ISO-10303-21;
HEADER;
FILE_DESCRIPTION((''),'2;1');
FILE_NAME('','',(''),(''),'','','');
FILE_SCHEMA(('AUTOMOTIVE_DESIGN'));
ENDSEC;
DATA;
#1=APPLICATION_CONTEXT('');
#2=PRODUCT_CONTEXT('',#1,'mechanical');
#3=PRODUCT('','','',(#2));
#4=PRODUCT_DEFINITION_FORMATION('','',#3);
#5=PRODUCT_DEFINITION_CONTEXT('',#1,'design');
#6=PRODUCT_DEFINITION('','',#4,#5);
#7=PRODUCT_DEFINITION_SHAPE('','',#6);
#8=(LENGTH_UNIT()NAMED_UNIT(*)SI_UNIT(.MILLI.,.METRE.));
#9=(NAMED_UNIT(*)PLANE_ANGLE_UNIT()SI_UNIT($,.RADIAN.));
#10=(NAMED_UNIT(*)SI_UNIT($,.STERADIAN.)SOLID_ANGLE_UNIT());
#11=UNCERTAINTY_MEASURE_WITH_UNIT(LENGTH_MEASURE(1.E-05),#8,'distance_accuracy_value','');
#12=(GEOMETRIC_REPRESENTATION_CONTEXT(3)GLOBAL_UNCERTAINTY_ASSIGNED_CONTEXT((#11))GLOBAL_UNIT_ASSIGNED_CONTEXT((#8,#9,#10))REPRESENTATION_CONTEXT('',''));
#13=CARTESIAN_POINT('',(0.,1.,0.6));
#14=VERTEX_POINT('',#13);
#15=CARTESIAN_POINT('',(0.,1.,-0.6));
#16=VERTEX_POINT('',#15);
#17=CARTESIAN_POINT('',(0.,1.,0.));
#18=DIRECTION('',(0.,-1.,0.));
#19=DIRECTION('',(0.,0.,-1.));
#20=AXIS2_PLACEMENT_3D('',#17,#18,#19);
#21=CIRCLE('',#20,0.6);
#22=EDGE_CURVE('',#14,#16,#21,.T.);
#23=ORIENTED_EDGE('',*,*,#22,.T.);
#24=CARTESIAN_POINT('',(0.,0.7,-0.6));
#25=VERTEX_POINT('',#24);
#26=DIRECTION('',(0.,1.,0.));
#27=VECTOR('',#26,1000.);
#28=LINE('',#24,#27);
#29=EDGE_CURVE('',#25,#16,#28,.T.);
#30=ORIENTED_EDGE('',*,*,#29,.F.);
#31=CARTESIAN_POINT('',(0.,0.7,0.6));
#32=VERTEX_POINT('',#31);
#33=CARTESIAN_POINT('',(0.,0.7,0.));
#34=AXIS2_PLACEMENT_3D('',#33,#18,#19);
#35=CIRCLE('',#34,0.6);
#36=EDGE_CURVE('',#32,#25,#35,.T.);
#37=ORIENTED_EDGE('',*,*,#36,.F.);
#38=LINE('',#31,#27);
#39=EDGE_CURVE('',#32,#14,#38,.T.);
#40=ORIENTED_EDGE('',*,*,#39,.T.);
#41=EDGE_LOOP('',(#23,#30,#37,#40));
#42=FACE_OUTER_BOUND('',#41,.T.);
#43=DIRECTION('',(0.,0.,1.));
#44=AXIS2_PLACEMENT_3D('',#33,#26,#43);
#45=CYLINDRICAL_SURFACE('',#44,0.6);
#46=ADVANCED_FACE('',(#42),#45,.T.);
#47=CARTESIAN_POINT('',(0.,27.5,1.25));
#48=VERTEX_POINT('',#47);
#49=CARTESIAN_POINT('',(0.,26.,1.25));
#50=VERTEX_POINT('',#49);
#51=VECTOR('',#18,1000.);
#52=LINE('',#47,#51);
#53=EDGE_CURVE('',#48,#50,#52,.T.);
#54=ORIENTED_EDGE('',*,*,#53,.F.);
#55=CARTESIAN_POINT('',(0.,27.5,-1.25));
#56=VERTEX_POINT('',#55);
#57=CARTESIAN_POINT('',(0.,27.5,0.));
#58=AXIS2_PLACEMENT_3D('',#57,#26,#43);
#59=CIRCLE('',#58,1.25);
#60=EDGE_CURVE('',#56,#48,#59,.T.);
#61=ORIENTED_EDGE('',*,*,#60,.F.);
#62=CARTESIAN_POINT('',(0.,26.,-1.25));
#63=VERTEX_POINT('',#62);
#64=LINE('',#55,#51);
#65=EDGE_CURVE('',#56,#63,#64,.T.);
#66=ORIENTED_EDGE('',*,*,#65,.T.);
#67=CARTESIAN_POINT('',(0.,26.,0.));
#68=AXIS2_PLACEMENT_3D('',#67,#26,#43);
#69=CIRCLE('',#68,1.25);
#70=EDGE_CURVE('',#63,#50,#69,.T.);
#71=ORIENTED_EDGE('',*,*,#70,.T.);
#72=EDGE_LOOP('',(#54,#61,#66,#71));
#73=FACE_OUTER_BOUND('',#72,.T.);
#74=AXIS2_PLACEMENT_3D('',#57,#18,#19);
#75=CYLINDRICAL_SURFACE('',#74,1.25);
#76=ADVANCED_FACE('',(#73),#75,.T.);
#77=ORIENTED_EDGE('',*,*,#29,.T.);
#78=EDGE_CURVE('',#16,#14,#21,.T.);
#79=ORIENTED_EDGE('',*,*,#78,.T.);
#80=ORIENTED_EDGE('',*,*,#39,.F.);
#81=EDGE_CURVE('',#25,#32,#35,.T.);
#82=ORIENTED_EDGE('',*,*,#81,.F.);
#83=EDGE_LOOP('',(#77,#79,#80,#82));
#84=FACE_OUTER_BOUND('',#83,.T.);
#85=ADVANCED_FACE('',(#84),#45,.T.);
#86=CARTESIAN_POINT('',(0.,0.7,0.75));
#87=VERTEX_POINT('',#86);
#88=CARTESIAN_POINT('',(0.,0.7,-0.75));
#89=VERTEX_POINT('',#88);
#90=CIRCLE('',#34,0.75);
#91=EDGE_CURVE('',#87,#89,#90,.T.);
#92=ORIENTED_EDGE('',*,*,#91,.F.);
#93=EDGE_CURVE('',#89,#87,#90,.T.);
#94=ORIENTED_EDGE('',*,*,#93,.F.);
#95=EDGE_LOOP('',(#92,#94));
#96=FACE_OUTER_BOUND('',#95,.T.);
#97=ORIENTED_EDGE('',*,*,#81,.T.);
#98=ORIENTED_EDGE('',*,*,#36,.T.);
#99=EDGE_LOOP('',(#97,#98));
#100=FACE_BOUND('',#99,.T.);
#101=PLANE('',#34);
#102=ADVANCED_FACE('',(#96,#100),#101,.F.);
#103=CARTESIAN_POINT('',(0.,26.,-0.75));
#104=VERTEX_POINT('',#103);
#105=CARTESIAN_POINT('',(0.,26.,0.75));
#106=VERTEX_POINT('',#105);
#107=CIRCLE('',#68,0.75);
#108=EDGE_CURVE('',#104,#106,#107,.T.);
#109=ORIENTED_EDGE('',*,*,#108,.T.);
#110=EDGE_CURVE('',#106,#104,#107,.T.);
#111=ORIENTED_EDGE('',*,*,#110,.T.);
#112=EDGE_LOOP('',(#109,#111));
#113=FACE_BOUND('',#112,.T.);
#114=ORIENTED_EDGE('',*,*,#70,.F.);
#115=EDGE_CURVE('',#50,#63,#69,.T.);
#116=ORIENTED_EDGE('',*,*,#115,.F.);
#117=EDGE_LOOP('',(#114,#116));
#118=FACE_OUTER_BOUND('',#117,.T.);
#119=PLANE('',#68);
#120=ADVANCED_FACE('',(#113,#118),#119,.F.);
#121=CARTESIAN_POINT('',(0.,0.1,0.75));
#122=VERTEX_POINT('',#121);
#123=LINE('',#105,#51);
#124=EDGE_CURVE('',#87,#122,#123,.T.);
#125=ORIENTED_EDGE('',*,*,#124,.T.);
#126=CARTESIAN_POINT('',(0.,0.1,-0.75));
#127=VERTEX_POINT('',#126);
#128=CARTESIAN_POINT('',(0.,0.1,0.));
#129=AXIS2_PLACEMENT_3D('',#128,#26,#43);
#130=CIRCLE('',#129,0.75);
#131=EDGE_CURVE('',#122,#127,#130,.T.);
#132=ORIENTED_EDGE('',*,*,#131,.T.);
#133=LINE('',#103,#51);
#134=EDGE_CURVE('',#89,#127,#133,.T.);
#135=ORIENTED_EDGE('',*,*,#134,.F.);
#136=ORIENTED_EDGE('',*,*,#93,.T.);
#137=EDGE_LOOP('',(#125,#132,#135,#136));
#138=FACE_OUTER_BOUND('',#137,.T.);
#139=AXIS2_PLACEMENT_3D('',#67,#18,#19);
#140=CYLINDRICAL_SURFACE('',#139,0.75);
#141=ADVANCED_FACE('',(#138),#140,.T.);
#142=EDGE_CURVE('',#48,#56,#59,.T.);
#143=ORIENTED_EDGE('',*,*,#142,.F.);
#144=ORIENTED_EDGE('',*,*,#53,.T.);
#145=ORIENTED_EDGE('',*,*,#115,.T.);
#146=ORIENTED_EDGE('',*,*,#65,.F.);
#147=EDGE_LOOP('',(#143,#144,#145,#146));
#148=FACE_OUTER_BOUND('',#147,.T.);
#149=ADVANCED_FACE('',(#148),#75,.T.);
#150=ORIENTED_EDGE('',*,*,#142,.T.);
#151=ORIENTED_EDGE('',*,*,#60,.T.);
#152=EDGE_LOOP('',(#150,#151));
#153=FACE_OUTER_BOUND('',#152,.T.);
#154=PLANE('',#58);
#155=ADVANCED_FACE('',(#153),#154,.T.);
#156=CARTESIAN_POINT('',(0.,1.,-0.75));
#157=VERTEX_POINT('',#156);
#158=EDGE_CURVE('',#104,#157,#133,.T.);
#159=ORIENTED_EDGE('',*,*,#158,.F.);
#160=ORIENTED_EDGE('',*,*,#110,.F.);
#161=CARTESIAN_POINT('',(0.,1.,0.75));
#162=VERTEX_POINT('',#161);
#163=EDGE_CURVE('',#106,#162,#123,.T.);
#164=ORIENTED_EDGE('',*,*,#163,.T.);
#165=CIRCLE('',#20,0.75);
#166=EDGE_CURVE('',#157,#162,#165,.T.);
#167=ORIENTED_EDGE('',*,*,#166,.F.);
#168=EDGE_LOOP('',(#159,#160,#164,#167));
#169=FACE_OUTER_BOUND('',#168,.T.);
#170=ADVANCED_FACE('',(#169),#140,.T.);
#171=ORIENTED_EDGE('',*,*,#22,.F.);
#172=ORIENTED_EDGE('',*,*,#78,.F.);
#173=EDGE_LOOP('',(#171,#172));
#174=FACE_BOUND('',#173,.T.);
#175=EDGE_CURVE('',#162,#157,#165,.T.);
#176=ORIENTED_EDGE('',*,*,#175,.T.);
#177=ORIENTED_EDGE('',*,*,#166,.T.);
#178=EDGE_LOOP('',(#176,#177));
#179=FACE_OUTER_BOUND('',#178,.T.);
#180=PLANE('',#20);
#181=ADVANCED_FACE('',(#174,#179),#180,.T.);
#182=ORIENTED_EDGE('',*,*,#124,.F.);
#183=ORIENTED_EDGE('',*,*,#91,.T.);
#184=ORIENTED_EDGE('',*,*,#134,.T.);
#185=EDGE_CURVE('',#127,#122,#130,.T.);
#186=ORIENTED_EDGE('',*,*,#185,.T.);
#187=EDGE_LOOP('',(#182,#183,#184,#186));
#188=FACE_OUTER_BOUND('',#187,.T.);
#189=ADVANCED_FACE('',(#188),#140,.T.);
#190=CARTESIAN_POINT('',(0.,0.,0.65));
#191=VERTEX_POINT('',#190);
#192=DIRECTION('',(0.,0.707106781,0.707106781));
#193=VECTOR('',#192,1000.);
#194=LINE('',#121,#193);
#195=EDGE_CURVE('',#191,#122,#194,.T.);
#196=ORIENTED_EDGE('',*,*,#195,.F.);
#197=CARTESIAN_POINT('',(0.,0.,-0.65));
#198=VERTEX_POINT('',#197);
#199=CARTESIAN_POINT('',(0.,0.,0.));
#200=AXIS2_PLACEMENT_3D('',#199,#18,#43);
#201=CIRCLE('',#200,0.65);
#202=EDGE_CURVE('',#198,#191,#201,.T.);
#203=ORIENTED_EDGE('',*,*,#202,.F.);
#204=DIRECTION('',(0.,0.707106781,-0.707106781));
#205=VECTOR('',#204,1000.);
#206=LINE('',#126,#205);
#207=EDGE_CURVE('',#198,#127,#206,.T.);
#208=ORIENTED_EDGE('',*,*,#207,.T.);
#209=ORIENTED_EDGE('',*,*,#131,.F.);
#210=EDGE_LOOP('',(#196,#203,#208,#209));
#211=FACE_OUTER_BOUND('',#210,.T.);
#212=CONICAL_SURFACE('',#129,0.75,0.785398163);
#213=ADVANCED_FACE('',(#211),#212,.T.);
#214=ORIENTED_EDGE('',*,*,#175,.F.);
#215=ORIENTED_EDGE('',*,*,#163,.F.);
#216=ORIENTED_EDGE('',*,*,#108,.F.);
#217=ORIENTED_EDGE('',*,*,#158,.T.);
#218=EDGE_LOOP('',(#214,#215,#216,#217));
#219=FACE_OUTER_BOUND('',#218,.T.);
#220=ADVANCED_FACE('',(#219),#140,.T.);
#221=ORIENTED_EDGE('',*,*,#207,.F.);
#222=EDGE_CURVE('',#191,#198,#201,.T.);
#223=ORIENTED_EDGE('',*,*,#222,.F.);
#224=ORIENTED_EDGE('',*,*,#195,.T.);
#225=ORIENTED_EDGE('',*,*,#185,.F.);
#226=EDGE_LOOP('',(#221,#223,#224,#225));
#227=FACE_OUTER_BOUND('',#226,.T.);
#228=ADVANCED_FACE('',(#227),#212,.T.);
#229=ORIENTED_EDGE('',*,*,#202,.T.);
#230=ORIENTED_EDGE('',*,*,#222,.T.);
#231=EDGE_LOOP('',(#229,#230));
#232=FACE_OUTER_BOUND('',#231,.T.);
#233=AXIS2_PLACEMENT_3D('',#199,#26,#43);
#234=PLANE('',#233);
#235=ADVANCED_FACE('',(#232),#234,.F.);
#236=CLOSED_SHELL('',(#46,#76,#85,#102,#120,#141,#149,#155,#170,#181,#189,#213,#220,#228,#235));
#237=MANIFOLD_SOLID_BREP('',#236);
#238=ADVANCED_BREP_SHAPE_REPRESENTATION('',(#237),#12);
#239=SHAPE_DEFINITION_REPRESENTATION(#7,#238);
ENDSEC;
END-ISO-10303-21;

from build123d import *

# Parameters (mm, degrees)
SKETCH1_R           = 0.75
BOSS_EXTRUDE1_DEPTH = 26
SKETCH2_R           = 1.25
BOSS_EXTRUDE2_DEPTH = 1.5
SKETCH3_OUTSIDE_W   = 10.046
SKETCH3_OUTSIDE_H   = 10.046
SKETCH3_OUTSIDE_R   = 0.6
CUT_EXTRUDE1_DEPTH  = 0.3
CHAMFER1_SIZE       = 0.1


with BuildPart() as part:
    # Sketch1 → Boss-Extrude1 (new body)
    with BuildSketch(Plane(origin=(0, 0, 0), x_dir=(1, 0, 0), z_dir=(0, 1, 0))):
        with Locations(Location((0, 0, 0), (0, 0, 270))):
            Circle(SKETCH1_R)
    extrude(amount=BOSS_EXTRUDE1_DEPTH)

    # Sketch2 → Boss-Extrude2 (add)
    with BuildSketch(Plane(origin=(0, 26, 0), x_dir=(1, 0, 0), z_dir=(0, 1, 0))):
        with Locations(Location((0, 0, 0), (0, 0, 270))):
            Circle(SKETCH2_R)
    extrude(amount=BOSS_EXTRUDE2_DEPTH)

    # Sketch3 outside → Cut-Extrude1 (cut)
    with BuildSketch(Plane(origin=(0, 1, 0), x_dir=(-1, 0, 0), z_dir=(0, -1, 0))):
        Rectangle(SKETCH3_OUTSIDE_W, SKETCH3_OUTSIDE_H)
        with Locations(Location((0, 0, 0), (0, 0, 90))):
            Circle(SKETCH3_OUTSIDE_R, mode=Mode.SUBTRACT)
    extrude(amount=CUT_EXTRUDE1_DEPTH, mode=Mode.SUBTRACT)

    # Chamfer1
    chamfer1_edges = [part.edges().sort_by_distance(p)[0] for p in [
        (0, 0, -0.75),
    ]]
    chamfer(chamfer1_edges, length=CHAMFER1_SIZE)


solid = part.part
